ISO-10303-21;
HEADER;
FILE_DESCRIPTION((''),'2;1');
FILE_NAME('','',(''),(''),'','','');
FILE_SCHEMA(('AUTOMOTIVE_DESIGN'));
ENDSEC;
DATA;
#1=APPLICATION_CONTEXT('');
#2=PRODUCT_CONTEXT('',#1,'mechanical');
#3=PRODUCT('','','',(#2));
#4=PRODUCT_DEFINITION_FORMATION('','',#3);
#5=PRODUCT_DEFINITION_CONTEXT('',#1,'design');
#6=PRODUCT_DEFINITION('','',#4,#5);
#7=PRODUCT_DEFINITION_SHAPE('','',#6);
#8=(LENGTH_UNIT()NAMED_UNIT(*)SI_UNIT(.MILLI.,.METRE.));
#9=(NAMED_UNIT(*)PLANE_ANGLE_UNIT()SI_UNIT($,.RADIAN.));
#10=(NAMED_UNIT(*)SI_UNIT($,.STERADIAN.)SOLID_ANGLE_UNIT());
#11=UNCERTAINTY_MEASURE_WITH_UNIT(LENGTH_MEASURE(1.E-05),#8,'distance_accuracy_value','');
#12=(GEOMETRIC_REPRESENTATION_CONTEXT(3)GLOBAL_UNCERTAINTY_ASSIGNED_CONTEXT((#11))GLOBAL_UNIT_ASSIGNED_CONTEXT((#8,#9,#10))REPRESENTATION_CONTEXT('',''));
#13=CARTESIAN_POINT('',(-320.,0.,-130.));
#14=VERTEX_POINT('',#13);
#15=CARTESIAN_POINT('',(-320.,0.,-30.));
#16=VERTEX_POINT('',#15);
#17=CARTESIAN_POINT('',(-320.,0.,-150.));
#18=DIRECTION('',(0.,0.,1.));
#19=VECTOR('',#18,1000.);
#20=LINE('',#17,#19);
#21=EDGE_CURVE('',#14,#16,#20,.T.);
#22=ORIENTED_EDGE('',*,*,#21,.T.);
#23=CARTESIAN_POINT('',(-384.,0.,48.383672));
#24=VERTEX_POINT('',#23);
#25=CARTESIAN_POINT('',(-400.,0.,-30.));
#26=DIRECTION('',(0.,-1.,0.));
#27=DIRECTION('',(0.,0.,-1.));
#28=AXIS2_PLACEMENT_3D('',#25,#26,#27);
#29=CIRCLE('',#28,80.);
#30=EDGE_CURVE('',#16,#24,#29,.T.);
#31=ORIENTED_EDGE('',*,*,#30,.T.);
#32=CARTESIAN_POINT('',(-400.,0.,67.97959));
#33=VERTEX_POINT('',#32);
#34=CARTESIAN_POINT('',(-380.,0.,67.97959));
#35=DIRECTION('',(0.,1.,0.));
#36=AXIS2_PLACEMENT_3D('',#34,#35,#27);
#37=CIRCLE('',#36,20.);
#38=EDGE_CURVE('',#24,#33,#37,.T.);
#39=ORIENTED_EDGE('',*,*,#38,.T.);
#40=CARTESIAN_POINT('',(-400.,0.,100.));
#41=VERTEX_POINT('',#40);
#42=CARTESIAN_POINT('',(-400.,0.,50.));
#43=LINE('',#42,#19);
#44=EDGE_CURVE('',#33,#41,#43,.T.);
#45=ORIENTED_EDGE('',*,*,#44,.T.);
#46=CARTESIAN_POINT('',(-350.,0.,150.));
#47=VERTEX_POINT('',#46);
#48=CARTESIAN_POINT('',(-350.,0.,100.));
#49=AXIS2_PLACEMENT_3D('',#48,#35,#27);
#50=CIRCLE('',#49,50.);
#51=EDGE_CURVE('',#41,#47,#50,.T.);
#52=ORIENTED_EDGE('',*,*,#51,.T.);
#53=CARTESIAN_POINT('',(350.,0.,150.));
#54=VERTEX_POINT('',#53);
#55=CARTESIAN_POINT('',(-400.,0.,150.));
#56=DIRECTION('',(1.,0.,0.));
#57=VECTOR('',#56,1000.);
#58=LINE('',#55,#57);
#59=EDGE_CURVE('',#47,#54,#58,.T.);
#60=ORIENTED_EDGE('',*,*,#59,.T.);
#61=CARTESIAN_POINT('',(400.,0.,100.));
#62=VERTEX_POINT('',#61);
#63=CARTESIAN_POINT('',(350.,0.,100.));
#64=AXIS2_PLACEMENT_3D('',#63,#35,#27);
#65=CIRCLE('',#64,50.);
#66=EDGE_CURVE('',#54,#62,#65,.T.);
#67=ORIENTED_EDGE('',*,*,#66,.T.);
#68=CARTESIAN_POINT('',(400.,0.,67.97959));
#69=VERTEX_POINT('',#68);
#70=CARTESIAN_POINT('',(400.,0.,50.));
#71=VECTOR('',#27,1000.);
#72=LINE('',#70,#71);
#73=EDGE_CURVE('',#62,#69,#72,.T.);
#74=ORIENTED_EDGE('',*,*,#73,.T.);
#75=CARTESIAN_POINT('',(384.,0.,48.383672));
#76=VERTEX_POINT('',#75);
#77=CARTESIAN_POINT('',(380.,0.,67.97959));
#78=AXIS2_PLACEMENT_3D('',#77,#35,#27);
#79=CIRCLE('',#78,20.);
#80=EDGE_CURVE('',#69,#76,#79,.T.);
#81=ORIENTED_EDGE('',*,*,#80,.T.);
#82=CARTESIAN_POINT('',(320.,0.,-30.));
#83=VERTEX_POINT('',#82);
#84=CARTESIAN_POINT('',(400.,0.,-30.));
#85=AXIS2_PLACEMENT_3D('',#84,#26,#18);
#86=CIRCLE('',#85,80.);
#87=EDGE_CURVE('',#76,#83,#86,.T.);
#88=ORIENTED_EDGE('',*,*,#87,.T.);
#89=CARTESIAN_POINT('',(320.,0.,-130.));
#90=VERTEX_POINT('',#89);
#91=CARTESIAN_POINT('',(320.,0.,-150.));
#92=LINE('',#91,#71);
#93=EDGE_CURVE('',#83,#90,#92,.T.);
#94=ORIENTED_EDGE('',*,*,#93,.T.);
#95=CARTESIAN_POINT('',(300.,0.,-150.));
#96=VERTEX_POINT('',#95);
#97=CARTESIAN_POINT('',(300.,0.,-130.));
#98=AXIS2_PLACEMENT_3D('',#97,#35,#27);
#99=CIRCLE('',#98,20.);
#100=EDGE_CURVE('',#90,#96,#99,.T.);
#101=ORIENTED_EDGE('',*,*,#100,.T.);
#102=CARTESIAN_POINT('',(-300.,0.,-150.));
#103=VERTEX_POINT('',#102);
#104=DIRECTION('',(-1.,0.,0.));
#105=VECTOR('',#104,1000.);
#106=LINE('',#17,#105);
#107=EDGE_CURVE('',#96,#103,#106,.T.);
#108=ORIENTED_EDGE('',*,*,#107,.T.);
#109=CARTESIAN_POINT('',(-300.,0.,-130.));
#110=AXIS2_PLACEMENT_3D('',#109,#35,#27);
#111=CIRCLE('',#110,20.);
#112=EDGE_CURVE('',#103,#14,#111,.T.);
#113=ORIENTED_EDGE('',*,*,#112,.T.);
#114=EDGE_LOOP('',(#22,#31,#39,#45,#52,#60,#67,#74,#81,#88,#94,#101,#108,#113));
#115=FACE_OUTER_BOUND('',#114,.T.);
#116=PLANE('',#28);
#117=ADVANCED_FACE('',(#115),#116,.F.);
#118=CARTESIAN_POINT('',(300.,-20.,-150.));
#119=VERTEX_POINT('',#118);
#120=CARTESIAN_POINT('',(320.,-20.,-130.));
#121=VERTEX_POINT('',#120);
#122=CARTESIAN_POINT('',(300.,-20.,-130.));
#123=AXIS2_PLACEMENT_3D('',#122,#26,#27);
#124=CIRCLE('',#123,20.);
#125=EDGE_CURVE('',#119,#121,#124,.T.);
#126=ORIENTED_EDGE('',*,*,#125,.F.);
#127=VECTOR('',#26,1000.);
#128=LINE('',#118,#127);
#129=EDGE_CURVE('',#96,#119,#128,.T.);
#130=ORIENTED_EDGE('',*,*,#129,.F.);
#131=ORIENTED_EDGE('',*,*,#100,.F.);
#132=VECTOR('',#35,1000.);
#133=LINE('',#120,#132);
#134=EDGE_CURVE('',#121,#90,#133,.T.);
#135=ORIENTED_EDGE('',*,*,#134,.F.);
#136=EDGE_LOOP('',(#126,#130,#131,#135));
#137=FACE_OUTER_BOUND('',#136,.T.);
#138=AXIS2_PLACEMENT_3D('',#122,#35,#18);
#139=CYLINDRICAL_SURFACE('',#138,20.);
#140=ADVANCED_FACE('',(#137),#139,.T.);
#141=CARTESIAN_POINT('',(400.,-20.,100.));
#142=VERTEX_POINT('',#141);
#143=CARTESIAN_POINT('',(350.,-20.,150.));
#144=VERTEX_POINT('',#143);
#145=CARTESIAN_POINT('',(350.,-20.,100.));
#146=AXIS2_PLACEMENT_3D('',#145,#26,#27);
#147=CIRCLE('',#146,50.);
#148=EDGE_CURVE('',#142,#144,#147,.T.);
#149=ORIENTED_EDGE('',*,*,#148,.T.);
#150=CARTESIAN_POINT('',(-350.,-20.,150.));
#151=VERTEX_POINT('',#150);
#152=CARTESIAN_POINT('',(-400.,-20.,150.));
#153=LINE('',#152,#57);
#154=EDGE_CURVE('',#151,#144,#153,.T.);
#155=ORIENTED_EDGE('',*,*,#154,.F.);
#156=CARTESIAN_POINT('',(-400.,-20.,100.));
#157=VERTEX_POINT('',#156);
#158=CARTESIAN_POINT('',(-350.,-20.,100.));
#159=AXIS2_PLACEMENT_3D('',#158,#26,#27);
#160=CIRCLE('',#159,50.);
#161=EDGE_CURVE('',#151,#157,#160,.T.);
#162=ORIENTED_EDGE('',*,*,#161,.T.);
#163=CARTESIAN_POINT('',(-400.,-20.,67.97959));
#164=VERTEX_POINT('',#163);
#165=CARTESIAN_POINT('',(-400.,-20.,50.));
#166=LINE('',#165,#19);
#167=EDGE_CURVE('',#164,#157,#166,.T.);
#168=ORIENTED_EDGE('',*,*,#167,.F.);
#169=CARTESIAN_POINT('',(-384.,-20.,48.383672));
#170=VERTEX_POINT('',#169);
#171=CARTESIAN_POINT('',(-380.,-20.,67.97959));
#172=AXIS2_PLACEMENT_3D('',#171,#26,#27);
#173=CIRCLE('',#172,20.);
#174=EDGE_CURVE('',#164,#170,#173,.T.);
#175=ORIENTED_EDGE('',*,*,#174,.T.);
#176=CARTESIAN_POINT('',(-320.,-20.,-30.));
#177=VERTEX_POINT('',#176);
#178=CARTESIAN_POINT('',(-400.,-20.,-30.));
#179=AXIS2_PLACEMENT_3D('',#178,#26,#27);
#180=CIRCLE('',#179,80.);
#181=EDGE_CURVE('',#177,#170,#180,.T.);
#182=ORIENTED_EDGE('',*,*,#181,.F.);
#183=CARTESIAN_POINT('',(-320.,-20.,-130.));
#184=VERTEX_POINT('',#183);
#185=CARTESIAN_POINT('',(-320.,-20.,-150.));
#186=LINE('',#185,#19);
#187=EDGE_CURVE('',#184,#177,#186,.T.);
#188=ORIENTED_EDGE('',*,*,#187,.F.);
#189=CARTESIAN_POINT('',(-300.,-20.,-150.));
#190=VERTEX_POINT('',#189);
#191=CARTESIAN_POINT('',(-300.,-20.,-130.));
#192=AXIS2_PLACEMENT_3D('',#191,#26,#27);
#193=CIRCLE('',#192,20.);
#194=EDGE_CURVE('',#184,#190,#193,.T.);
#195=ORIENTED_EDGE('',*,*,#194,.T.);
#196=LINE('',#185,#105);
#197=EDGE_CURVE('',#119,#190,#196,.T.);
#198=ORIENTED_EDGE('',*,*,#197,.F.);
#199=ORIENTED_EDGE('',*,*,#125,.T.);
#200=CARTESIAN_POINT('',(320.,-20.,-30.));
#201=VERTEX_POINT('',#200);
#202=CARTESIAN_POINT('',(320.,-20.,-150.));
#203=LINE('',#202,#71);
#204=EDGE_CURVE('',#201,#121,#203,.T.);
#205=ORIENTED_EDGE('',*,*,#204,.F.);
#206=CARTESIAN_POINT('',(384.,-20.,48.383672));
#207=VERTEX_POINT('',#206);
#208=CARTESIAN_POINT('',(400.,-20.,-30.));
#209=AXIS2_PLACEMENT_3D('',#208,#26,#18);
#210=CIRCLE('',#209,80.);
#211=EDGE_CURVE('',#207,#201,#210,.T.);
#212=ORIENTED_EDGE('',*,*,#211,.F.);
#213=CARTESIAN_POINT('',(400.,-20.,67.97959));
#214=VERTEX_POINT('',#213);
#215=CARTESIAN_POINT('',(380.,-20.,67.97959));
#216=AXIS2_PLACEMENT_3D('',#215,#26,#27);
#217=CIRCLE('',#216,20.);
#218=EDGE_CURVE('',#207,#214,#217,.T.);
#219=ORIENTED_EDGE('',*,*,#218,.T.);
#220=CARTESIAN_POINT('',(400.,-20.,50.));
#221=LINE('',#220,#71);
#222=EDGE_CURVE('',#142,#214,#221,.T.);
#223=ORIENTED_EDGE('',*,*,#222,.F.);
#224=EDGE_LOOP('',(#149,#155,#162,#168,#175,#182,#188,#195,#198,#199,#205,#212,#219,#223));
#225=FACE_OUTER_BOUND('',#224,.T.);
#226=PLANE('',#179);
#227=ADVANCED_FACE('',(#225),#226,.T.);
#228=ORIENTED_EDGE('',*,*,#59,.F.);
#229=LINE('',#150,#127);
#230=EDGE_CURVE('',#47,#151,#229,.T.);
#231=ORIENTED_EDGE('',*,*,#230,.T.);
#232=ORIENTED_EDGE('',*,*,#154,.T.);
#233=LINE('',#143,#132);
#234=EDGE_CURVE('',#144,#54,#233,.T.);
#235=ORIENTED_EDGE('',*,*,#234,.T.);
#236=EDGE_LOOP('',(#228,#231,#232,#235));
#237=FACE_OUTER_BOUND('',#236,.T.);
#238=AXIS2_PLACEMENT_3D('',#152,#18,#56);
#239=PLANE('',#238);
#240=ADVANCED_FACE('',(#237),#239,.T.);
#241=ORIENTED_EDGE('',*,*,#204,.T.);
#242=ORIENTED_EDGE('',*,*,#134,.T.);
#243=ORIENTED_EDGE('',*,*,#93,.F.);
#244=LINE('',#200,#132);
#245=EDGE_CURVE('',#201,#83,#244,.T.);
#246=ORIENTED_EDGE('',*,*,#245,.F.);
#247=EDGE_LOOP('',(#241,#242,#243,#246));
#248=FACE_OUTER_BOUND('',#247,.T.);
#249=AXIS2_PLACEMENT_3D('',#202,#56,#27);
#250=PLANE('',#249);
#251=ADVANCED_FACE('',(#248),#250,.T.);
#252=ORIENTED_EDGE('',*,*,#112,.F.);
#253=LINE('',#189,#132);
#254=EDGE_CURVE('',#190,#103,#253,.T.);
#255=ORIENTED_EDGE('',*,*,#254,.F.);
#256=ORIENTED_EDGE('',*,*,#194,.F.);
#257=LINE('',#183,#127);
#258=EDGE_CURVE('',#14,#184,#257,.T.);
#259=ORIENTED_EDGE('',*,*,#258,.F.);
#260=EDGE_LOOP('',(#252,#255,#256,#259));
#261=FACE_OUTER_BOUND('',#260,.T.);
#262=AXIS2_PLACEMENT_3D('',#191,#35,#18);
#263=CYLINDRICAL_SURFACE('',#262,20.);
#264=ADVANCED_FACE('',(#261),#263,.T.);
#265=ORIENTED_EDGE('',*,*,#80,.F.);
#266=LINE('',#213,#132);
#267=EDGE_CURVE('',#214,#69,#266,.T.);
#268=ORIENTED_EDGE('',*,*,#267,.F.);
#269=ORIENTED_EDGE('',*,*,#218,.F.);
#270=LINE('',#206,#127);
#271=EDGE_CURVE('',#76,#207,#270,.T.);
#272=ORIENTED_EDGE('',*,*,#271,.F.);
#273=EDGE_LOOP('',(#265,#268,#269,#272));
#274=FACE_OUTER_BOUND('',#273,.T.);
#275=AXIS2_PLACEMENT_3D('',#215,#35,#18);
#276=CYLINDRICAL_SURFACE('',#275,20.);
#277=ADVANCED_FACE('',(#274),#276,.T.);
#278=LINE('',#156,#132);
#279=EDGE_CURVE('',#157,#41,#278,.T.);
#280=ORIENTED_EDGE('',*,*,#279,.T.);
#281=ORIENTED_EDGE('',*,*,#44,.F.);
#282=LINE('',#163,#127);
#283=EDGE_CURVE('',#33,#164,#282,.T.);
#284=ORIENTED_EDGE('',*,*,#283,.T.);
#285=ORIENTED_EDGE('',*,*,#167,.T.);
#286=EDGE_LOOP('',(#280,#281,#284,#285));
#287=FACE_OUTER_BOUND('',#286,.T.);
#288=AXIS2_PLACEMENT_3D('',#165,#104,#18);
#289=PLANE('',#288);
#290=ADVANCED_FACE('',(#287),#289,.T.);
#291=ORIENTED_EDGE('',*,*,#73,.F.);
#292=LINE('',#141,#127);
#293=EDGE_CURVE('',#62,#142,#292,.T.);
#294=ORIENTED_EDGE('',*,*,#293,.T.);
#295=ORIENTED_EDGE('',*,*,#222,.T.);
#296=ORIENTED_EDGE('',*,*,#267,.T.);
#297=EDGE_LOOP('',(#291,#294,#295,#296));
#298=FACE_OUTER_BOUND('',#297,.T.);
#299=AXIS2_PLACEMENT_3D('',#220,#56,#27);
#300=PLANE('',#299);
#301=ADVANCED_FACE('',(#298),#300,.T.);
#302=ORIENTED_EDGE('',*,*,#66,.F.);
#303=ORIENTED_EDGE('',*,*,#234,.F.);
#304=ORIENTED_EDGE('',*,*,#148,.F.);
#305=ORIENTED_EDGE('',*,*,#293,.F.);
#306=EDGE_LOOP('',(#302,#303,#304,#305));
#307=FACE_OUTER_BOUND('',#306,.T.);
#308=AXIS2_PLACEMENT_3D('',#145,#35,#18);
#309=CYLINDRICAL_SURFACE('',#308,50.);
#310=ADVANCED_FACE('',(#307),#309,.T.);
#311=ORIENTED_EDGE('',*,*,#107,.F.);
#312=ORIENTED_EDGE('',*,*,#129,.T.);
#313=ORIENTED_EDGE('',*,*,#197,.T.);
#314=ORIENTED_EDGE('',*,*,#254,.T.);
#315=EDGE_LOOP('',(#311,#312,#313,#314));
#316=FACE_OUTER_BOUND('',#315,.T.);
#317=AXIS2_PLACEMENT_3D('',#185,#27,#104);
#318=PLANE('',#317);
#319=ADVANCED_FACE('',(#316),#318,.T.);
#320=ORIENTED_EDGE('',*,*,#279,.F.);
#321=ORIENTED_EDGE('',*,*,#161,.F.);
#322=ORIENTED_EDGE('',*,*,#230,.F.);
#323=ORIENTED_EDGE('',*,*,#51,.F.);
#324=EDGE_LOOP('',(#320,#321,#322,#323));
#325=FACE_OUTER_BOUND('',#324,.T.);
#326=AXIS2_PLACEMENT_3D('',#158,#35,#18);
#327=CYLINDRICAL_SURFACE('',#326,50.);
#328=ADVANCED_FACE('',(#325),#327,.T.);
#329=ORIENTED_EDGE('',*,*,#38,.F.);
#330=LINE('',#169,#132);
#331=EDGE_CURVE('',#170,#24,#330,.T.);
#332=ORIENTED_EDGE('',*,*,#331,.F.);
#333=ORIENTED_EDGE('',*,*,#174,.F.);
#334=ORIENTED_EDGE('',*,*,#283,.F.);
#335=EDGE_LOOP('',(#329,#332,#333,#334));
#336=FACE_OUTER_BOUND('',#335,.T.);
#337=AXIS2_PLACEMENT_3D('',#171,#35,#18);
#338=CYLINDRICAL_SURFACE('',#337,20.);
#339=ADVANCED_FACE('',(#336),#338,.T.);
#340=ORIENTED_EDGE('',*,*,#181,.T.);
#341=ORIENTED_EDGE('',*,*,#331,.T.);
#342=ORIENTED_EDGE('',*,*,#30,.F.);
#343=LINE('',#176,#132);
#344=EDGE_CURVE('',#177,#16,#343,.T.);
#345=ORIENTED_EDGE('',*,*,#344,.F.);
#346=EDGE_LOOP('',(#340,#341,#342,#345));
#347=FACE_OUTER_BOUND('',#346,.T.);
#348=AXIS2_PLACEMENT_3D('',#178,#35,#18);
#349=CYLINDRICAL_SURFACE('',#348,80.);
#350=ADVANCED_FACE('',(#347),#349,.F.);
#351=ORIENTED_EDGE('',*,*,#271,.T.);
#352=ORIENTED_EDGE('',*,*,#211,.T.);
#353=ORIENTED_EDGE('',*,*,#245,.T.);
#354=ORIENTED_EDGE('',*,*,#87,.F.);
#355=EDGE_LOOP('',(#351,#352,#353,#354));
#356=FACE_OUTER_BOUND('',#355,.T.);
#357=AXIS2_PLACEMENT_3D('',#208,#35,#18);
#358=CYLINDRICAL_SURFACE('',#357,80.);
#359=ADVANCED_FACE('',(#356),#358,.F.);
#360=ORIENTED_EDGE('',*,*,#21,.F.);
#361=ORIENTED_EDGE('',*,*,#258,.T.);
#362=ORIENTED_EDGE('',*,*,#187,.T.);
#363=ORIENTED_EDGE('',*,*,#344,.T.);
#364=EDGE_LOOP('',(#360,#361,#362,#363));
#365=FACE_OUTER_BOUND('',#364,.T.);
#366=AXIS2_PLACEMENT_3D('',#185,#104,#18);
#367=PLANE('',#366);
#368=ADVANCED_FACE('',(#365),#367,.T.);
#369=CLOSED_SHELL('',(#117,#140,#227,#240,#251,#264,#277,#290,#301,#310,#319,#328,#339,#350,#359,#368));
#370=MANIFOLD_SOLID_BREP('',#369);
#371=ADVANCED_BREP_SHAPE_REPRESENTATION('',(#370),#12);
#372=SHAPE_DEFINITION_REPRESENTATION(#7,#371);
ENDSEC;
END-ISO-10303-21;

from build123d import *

# Parameters (mm, degrees)
BOSS_EXTRUDE1_DEPTH = 20
FILLET1_R           = 50
FILLET2_R           = 20


with BuildPart() as part:
    # Sketch1 → Boss-Extrude1 (new body)
    with BuildSketch(Plane(origin=(0, 0, 0), x_dir=(1, 0, 0), z_dir=(0, 1, 0))):
        with BuildLine():
            Line((-320, 150), (-320, 30))
            ThreePointArc((-320, 30), (-343.431457505, -26.568542495), (-400, -50))
            Line((-400, -50), (-400, -150))
            Line((-400, -150), (400, -150))
            Line((400, -150), (400, -50))
            ThreePointArc((400, -50), (343.431457505, -26.568542495), (320, 30))
            Line((320, 30), (320, 150))
            Line((320, 150), (-320, 150))
        make_face()
    extrude(amount=-BOSS_EXTRUDE1_DEPTH)

    # Fillet1
    fillet1_edges = [part.edges().sort_by_distance(p)[0] for p in [
        (400, -10, 150),
        (-400, -10, 150),
    ]]
    fillet(fillet1_edges, radius=FILLET1_R)

    # Fillet2
    fillet2_edges = [part.edges().sort_by_distance(p)[0] for p in [
        (-400, -10, 50),
        (-320, -10, -150),
        (320, -10, -150),
        (400, -10, 50),
    ]]
    fillet(fillet2_edges, radius=FILLET2_R)


solid = part.part
